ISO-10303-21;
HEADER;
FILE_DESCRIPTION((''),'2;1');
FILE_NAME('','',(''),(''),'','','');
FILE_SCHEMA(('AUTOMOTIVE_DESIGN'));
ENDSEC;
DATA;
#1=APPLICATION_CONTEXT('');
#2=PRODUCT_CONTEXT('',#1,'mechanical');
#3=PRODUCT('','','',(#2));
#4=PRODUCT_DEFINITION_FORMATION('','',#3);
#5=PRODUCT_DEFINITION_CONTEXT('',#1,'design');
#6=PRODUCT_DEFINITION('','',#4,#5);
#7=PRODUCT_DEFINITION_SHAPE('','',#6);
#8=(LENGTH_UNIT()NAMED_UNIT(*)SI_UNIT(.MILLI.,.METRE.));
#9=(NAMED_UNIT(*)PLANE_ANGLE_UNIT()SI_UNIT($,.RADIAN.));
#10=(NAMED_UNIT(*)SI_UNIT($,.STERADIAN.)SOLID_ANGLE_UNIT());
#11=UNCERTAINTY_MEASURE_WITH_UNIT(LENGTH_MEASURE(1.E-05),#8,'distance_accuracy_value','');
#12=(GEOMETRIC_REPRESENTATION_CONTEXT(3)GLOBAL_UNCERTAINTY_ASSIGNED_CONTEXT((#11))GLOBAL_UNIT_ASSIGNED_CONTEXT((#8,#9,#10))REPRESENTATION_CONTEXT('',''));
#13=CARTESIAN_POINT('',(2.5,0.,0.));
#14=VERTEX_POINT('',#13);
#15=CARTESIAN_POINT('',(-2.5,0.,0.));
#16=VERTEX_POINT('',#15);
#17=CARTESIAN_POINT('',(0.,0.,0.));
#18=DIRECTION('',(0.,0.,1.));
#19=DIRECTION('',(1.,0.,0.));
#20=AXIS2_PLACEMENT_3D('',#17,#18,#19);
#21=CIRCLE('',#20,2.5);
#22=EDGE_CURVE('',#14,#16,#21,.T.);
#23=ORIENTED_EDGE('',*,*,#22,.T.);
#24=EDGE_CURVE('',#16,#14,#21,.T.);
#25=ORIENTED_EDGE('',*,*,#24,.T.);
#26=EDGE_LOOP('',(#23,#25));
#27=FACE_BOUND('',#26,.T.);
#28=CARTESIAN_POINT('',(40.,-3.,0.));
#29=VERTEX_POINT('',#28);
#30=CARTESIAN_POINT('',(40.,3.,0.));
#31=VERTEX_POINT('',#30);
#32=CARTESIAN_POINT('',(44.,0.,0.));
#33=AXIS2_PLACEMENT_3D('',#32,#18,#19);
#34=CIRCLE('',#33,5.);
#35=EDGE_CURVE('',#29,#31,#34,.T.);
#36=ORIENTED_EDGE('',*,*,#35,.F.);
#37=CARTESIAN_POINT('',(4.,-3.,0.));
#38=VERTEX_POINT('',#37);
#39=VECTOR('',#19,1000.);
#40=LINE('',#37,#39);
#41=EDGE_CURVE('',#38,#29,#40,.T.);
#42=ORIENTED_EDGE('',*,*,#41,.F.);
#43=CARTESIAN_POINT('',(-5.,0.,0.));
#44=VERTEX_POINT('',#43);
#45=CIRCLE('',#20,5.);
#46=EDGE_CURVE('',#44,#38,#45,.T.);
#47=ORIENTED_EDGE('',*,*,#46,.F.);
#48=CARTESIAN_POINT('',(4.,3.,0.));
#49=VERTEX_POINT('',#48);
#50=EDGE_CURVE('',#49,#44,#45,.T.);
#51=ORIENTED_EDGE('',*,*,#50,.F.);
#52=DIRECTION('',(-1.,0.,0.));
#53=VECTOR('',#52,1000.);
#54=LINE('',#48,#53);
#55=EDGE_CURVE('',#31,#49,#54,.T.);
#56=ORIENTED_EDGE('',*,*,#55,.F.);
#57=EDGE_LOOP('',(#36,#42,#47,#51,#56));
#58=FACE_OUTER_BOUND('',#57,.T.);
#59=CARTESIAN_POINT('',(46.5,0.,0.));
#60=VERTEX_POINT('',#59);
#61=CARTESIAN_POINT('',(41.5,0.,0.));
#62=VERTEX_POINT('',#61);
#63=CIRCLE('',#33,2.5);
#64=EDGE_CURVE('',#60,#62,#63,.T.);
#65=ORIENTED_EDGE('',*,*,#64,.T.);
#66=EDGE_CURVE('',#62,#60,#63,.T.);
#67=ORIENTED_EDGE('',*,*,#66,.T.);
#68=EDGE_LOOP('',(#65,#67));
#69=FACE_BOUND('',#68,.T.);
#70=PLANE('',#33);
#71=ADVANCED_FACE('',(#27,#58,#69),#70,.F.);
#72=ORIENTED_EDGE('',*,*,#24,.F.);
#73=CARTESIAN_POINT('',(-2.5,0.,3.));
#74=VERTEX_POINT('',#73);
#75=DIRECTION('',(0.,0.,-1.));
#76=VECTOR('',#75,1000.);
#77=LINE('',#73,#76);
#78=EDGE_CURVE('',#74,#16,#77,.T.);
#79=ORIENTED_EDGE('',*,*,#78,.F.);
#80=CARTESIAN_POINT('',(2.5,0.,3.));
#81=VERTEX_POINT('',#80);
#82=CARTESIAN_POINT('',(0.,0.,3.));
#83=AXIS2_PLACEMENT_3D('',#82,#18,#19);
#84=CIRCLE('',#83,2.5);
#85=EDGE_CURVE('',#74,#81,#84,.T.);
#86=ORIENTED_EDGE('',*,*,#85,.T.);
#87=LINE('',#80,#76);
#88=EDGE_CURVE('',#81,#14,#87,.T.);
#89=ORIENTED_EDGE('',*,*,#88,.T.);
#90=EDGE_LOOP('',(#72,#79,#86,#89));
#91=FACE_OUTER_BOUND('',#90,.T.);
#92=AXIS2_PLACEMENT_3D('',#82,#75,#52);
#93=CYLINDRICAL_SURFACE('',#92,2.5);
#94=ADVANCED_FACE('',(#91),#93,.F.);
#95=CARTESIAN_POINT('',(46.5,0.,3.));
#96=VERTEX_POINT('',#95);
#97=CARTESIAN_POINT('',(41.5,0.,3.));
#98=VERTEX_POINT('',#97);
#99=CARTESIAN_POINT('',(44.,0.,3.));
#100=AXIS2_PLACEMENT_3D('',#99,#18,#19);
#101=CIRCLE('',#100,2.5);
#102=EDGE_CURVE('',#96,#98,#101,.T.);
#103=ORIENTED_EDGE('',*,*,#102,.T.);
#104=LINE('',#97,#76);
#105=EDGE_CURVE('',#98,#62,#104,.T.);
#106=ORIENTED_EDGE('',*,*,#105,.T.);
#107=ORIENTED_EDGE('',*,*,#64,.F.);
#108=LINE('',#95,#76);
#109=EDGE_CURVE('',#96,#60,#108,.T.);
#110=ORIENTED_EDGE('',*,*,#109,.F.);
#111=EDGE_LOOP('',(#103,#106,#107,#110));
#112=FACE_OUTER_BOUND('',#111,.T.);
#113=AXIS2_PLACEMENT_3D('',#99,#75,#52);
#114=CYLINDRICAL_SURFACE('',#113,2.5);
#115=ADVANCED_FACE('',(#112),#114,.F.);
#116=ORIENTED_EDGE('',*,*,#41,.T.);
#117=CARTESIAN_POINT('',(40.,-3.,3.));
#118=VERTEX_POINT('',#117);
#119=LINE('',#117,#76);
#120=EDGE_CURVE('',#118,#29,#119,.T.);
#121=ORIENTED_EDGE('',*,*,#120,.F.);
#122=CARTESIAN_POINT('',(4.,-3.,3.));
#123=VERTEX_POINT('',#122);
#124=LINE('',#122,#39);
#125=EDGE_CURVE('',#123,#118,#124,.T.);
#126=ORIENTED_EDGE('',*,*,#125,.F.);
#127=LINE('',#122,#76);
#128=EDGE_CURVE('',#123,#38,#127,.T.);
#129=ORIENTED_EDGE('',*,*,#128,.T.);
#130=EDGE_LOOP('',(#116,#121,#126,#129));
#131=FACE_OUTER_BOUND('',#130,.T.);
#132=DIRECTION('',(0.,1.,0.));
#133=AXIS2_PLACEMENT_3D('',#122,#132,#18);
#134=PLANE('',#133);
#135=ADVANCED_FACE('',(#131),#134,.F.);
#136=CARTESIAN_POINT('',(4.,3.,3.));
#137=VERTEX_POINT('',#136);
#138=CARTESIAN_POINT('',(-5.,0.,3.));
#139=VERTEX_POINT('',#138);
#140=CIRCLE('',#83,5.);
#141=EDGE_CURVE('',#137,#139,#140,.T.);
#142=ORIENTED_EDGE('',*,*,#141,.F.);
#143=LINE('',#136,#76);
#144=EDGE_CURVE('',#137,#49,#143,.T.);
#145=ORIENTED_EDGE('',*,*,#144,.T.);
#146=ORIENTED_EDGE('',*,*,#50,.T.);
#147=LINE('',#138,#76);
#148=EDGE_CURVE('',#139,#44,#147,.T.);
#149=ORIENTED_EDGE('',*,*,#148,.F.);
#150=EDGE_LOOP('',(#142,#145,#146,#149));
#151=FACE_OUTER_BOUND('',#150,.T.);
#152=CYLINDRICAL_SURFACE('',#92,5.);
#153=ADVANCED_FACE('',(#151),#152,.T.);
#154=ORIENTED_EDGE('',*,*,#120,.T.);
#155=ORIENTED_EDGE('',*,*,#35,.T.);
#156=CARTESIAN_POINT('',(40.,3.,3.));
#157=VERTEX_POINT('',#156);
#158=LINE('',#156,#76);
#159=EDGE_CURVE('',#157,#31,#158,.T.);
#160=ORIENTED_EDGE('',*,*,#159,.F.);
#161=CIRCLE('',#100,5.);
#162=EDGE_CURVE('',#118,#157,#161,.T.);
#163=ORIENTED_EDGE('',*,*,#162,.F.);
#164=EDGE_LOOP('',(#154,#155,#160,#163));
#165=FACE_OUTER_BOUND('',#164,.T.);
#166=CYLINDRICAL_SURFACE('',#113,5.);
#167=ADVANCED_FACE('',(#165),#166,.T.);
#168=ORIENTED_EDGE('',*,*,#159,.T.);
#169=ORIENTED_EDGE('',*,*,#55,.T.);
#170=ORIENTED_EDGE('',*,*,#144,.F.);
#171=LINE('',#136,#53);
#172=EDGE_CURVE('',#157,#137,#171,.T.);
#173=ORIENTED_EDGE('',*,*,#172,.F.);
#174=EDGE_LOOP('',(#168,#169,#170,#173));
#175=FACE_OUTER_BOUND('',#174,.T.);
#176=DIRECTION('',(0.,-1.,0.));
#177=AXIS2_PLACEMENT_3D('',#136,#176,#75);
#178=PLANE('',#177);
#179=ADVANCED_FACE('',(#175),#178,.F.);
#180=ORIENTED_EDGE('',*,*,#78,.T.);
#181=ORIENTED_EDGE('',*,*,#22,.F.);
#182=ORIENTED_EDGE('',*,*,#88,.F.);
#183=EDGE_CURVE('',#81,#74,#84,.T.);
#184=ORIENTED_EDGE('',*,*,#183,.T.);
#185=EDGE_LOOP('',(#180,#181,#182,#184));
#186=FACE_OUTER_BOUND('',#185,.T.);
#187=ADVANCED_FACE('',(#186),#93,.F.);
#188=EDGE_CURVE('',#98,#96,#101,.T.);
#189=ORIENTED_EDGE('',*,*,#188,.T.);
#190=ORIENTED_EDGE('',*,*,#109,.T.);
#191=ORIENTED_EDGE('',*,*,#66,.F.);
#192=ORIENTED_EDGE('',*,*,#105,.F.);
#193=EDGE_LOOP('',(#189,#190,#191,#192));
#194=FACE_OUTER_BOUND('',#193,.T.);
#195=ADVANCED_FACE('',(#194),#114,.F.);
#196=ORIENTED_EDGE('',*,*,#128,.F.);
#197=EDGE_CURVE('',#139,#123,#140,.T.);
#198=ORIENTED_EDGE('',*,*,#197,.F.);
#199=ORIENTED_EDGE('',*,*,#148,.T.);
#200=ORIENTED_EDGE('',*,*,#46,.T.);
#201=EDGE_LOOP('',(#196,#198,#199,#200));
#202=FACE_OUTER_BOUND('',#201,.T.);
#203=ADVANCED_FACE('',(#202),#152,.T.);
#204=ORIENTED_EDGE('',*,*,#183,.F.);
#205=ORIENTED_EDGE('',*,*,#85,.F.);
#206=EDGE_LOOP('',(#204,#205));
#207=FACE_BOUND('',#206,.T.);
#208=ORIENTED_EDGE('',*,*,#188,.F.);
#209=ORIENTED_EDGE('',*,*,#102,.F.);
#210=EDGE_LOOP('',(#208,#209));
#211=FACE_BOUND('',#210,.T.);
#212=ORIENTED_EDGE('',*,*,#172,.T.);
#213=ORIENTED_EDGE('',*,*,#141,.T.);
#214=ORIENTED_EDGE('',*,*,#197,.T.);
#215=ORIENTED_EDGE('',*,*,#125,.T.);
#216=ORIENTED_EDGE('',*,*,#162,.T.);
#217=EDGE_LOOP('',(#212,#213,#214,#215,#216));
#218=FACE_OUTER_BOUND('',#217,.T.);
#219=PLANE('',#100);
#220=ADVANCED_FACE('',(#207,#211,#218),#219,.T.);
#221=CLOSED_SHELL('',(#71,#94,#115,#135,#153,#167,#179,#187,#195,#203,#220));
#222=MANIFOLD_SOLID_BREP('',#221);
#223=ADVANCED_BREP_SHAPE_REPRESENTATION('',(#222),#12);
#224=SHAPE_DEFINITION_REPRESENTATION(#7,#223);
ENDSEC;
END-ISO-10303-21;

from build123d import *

# Parameters (mm, degrees)
SKETCH1_R           = 2.5
BOSS_EXTRUDE1_DEPTH = 3


with BuildPart() as part:
    # Sketch1 → Boss-Extrude1 (new body)
    with BuildSketch(Plane.XY):
        with BuildLine():
            Line((4, 3), (40, 3))
            ThreePointArc((40, 3), (49, 0), (40, -3))
            Line((40, -3), (4, -3))
            ThreePointArc((4, -3), (-5, 0), (4, 3))
        make_face()
        Circle(SKETCH1_R, mode=Mode.SUBTRACT)
        with Locations((44, 0)):
            Circle(SKETCH1_R, mode=Mode.SUBTRACT)
    extrude(amount=BOSS_EXTRUDE1_DEPTH)


solid = part.part
